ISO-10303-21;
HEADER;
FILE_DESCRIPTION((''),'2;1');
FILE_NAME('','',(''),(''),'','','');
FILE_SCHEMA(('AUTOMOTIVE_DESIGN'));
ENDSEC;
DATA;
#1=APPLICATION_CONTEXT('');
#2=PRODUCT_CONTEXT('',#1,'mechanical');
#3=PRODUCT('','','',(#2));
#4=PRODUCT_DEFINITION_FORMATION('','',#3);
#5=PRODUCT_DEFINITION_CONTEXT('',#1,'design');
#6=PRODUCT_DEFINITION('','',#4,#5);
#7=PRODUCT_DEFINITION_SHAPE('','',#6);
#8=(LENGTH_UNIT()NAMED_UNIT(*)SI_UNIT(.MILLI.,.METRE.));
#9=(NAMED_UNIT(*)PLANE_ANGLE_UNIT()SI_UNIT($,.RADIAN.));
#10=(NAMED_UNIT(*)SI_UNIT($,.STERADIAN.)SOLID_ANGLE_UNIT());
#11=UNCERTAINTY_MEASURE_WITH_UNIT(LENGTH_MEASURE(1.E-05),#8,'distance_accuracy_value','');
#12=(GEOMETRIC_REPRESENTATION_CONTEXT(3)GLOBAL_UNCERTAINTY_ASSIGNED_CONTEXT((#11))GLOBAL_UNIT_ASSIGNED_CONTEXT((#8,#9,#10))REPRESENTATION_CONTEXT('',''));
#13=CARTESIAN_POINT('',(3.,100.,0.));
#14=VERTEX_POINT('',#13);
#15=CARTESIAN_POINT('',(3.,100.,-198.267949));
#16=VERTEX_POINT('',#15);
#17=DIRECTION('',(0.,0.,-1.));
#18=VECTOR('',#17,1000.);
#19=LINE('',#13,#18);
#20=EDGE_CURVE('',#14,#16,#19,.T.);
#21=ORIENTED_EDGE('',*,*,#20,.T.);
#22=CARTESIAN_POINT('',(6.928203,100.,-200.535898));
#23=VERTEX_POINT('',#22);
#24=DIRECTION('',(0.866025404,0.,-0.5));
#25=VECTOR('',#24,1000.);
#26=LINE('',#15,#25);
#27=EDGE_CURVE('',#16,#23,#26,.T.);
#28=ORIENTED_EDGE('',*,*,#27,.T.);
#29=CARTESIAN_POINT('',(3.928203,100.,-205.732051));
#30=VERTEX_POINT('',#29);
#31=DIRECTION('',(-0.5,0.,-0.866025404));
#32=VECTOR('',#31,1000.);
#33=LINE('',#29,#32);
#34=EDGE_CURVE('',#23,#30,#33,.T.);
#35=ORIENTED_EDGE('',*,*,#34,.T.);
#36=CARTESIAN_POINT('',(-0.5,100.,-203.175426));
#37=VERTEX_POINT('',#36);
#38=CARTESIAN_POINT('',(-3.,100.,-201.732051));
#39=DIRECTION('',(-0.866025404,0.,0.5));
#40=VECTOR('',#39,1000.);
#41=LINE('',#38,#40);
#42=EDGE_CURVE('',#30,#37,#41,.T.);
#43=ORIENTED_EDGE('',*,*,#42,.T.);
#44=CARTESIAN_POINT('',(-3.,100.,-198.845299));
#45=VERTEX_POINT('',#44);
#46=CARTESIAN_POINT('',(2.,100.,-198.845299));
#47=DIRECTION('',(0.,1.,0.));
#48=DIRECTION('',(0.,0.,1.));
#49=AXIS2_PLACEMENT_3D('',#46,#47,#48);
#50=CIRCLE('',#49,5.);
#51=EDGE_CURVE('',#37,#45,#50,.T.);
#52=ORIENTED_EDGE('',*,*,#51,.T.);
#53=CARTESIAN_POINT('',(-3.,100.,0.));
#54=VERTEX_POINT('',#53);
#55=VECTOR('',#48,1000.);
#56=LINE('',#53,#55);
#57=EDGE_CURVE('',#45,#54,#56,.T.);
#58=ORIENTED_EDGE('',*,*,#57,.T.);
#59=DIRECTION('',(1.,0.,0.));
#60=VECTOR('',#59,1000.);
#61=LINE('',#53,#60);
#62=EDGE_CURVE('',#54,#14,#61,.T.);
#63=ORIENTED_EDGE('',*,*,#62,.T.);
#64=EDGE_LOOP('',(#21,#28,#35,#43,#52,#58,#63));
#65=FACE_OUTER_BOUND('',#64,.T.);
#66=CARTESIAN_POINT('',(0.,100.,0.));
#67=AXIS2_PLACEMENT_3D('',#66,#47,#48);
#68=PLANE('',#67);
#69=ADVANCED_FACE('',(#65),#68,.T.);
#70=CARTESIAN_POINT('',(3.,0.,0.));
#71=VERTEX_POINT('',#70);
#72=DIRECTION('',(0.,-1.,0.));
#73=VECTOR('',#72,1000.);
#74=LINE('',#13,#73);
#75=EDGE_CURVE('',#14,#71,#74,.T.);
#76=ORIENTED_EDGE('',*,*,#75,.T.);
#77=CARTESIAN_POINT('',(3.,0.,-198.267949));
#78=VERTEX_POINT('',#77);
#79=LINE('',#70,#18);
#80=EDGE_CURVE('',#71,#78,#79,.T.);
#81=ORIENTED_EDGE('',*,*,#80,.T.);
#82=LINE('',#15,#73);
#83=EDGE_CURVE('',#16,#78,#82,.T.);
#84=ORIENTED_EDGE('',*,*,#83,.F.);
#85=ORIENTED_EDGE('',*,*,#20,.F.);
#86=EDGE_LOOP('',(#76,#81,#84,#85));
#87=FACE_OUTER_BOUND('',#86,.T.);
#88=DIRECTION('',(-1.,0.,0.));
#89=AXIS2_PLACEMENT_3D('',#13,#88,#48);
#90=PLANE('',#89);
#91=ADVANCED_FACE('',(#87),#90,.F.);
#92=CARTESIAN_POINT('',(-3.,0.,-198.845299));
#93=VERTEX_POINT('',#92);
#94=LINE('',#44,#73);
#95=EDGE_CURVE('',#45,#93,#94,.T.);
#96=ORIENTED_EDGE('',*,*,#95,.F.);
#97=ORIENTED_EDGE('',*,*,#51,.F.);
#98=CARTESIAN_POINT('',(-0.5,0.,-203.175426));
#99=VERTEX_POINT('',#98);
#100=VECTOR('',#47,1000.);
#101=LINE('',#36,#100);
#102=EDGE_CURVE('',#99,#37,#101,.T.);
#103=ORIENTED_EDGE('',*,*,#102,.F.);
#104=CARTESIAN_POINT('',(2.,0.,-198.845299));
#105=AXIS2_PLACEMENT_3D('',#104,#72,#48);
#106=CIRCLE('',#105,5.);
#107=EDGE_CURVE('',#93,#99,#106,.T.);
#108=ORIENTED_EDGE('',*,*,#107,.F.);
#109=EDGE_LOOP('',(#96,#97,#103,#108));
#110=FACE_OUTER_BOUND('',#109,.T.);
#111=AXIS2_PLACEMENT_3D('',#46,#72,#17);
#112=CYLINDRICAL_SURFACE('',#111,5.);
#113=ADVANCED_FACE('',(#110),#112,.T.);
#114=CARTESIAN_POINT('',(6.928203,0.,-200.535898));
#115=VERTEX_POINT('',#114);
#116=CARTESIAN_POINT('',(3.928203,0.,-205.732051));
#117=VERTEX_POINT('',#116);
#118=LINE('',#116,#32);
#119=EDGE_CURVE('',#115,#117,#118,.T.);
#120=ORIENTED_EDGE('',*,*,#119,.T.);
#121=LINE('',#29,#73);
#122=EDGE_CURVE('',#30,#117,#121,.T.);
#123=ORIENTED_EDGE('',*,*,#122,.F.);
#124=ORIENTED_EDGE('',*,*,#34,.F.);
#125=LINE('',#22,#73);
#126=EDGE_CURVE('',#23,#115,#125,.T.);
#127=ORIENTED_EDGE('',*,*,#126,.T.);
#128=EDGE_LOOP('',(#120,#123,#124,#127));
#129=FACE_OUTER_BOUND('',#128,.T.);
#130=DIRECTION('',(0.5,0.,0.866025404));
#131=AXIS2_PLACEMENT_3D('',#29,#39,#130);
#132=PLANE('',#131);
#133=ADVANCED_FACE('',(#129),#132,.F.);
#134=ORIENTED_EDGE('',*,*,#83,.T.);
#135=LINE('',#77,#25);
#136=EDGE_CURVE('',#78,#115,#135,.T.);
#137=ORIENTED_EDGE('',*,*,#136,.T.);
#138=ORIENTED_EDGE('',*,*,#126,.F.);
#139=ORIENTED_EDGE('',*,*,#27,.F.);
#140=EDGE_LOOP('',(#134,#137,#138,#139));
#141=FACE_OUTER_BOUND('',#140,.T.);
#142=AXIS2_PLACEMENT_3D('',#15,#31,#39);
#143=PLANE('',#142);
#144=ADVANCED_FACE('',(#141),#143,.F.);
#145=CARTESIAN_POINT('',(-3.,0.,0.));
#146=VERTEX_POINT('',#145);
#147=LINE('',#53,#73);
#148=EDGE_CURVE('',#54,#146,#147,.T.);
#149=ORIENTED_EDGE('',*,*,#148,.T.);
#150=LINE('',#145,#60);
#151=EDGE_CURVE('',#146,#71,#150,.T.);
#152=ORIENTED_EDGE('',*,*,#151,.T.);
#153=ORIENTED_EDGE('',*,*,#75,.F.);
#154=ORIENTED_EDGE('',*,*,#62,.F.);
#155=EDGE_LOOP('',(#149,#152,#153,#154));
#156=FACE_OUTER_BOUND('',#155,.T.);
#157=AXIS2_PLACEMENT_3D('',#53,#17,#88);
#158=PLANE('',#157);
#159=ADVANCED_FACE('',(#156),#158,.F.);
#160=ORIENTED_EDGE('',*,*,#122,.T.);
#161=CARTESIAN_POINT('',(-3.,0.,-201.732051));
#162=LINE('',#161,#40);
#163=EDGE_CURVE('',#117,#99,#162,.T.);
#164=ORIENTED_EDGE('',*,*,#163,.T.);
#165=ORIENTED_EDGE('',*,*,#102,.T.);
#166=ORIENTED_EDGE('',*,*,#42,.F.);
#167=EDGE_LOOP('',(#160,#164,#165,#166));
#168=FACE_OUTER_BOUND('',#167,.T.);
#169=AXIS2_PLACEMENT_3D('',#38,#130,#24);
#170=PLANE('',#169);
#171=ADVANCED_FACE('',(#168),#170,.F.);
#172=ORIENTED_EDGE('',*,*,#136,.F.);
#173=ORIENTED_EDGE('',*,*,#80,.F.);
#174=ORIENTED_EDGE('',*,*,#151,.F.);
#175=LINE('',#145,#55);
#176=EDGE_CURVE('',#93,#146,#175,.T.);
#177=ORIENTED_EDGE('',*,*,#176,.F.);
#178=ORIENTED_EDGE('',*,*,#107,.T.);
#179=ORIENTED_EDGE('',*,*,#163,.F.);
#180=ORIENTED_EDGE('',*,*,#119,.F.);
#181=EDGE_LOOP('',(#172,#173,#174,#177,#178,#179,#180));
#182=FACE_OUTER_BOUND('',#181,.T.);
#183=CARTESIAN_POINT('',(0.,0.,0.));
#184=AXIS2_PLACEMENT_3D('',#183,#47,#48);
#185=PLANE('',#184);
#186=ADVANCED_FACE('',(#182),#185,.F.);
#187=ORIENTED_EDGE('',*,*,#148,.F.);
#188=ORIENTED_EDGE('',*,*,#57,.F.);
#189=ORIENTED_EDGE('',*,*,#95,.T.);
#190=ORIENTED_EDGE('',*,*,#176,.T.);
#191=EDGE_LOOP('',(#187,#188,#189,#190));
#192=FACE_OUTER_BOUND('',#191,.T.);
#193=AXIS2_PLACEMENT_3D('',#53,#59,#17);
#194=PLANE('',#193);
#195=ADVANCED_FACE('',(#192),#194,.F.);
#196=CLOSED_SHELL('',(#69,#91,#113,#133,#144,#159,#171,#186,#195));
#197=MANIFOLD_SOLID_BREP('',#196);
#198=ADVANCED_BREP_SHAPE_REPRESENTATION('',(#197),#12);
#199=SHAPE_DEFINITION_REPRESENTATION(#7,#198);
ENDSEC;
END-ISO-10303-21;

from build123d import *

# Parameters (mm, degrees)
EXTRUDE_1_DEPTH = 100
FILLET_1_R      = 5


with BuildPart() as part:
    # 草图1 → 凸台-拉伸1 (new body)
    with BuildSketch(Plane(origin=(0, 0, 0), x_dir=(1, 0, 0), z_dir=(0, 1, 0))):
        Polygon((3, 0), (3, 198.267949192), (6.92820323, 200.535898385), (3.92820323, 205.732050808), (-3, 201.732050808), (-3, 0), align=None)
    extrude(amount=EXTRUDE_1_DEPTH)

    # 圆角1
    fillet_1_edges = [part.edges().sort_by_distance(p)[0] for p in [
        (-3, 50, -201.732050808),
    ]]
    fillet(fillet_1_edges, radius=FILLET_1_R)


solid = part.part
